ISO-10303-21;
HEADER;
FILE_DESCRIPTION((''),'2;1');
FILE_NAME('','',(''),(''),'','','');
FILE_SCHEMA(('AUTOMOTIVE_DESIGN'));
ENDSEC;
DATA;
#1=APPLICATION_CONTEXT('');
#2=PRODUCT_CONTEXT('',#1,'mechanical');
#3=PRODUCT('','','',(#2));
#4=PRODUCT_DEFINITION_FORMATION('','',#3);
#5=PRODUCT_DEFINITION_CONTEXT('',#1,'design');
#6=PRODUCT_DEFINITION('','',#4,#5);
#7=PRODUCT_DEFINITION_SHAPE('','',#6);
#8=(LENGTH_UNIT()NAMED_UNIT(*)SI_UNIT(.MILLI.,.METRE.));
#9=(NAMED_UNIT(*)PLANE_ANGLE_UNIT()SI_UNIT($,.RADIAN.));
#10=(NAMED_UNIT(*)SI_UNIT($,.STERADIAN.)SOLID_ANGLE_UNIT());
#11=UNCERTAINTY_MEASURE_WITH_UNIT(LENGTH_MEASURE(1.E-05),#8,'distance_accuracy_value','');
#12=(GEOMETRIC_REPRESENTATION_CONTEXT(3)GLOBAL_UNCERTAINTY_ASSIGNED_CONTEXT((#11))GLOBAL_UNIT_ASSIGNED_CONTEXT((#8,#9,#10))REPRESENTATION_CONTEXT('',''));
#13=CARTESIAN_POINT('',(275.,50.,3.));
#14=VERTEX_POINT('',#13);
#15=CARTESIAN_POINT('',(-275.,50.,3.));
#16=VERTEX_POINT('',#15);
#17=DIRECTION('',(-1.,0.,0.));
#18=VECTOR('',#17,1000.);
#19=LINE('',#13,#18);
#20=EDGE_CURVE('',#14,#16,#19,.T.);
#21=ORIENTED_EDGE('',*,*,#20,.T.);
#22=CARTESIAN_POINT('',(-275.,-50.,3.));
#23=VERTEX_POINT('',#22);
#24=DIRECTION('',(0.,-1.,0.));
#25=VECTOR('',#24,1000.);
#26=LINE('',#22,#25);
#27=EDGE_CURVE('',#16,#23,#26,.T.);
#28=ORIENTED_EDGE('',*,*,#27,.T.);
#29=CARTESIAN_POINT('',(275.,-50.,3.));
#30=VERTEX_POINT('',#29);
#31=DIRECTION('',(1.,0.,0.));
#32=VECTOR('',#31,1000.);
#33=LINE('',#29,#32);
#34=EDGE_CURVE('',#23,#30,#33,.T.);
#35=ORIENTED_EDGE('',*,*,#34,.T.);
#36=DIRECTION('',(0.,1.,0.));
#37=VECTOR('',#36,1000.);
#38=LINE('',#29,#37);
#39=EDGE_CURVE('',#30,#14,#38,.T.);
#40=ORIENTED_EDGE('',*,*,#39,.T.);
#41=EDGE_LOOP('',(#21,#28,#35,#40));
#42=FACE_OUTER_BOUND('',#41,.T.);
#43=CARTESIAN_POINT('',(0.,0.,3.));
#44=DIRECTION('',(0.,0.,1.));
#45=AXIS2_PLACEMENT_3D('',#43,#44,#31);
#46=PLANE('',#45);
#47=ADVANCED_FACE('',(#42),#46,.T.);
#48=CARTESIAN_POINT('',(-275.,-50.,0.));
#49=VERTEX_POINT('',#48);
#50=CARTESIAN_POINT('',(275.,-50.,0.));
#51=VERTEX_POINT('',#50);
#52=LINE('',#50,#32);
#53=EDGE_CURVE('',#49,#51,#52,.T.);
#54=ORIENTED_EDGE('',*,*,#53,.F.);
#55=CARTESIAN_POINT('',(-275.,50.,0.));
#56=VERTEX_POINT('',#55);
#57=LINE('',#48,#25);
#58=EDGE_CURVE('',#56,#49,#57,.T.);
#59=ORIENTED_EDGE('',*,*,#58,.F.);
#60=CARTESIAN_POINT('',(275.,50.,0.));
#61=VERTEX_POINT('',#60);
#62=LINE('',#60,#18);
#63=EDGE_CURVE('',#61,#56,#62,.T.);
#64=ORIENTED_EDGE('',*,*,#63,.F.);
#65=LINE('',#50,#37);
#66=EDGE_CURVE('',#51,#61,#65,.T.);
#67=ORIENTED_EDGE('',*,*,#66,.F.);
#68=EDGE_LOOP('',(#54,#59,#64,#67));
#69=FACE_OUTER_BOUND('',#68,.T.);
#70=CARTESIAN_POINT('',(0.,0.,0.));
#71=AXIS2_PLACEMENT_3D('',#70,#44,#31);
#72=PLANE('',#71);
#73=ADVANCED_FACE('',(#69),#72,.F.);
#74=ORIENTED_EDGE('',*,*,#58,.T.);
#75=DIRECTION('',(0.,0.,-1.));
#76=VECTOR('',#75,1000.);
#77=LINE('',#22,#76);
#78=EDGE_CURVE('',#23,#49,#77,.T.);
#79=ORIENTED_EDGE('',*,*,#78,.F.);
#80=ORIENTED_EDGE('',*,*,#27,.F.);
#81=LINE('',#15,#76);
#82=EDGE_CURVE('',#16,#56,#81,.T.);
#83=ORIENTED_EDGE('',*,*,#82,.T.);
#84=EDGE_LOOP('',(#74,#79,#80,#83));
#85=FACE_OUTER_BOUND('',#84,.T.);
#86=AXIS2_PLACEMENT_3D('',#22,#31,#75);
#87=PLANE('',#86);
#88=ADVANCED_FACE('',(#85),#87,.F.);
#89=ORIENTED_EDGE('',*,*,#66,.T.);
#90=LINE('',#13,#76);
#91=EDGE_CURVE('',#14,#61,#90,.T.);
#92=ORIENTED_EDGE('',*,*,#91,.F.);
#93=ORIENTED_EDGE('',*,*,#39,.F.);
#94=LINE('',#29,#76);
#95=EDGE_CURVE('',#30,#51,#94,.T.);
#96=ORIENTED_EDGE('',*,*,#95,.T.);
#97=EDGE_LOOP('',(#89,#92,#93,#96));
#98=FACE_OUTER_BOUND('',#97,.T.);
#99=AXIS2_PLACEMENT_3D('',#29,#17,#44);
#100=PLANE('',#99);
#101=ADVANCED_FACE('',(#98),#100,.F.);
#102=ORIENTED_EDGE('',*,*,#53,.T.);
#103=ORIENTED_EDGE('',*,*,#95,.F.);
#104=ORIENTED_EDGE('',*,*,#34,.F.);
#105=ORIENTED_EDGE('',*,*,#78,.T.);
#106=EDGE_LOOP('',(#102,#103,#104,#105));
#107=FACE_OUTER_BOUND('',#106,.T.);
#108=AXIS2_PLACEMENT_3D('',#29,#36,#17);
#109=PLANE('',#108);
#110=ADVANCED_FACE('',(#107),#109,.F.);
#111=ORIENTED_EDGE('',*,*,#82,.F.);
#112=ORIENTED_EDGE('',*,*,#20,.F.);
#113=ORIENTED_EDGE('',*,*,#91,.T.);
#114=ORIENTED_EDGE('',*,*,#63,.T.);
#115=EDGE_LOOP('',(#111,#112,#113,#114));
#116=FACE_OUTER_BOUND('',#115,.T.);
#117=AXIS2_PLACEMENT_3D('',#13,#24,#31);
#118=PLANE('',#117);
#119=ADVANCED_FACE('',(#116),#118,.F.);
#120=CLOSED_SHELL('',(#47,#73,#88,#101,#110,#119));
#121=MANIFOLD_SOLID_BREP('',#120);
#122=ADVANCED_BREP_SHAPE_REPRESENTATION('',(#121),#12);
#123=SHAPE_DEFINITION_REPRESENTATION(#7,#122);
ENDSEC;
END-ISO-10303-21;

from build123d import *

# Parameters (mm, degrees)
SKETCH_1_W      = 550
SKETCH_1_H      = 100
EXTRUDE_1_DEPTH = 3


with BuildPart() as part:
    # 草图1 → 凸台-拉伸1 (new body)
    with BuildSketch(Plane.XY):
        Rectangle(SKETCH_1_W, SKETCH_1_H)
    extrude(amount=EXTRUDE_1_DEPTH)


solid = part.part
